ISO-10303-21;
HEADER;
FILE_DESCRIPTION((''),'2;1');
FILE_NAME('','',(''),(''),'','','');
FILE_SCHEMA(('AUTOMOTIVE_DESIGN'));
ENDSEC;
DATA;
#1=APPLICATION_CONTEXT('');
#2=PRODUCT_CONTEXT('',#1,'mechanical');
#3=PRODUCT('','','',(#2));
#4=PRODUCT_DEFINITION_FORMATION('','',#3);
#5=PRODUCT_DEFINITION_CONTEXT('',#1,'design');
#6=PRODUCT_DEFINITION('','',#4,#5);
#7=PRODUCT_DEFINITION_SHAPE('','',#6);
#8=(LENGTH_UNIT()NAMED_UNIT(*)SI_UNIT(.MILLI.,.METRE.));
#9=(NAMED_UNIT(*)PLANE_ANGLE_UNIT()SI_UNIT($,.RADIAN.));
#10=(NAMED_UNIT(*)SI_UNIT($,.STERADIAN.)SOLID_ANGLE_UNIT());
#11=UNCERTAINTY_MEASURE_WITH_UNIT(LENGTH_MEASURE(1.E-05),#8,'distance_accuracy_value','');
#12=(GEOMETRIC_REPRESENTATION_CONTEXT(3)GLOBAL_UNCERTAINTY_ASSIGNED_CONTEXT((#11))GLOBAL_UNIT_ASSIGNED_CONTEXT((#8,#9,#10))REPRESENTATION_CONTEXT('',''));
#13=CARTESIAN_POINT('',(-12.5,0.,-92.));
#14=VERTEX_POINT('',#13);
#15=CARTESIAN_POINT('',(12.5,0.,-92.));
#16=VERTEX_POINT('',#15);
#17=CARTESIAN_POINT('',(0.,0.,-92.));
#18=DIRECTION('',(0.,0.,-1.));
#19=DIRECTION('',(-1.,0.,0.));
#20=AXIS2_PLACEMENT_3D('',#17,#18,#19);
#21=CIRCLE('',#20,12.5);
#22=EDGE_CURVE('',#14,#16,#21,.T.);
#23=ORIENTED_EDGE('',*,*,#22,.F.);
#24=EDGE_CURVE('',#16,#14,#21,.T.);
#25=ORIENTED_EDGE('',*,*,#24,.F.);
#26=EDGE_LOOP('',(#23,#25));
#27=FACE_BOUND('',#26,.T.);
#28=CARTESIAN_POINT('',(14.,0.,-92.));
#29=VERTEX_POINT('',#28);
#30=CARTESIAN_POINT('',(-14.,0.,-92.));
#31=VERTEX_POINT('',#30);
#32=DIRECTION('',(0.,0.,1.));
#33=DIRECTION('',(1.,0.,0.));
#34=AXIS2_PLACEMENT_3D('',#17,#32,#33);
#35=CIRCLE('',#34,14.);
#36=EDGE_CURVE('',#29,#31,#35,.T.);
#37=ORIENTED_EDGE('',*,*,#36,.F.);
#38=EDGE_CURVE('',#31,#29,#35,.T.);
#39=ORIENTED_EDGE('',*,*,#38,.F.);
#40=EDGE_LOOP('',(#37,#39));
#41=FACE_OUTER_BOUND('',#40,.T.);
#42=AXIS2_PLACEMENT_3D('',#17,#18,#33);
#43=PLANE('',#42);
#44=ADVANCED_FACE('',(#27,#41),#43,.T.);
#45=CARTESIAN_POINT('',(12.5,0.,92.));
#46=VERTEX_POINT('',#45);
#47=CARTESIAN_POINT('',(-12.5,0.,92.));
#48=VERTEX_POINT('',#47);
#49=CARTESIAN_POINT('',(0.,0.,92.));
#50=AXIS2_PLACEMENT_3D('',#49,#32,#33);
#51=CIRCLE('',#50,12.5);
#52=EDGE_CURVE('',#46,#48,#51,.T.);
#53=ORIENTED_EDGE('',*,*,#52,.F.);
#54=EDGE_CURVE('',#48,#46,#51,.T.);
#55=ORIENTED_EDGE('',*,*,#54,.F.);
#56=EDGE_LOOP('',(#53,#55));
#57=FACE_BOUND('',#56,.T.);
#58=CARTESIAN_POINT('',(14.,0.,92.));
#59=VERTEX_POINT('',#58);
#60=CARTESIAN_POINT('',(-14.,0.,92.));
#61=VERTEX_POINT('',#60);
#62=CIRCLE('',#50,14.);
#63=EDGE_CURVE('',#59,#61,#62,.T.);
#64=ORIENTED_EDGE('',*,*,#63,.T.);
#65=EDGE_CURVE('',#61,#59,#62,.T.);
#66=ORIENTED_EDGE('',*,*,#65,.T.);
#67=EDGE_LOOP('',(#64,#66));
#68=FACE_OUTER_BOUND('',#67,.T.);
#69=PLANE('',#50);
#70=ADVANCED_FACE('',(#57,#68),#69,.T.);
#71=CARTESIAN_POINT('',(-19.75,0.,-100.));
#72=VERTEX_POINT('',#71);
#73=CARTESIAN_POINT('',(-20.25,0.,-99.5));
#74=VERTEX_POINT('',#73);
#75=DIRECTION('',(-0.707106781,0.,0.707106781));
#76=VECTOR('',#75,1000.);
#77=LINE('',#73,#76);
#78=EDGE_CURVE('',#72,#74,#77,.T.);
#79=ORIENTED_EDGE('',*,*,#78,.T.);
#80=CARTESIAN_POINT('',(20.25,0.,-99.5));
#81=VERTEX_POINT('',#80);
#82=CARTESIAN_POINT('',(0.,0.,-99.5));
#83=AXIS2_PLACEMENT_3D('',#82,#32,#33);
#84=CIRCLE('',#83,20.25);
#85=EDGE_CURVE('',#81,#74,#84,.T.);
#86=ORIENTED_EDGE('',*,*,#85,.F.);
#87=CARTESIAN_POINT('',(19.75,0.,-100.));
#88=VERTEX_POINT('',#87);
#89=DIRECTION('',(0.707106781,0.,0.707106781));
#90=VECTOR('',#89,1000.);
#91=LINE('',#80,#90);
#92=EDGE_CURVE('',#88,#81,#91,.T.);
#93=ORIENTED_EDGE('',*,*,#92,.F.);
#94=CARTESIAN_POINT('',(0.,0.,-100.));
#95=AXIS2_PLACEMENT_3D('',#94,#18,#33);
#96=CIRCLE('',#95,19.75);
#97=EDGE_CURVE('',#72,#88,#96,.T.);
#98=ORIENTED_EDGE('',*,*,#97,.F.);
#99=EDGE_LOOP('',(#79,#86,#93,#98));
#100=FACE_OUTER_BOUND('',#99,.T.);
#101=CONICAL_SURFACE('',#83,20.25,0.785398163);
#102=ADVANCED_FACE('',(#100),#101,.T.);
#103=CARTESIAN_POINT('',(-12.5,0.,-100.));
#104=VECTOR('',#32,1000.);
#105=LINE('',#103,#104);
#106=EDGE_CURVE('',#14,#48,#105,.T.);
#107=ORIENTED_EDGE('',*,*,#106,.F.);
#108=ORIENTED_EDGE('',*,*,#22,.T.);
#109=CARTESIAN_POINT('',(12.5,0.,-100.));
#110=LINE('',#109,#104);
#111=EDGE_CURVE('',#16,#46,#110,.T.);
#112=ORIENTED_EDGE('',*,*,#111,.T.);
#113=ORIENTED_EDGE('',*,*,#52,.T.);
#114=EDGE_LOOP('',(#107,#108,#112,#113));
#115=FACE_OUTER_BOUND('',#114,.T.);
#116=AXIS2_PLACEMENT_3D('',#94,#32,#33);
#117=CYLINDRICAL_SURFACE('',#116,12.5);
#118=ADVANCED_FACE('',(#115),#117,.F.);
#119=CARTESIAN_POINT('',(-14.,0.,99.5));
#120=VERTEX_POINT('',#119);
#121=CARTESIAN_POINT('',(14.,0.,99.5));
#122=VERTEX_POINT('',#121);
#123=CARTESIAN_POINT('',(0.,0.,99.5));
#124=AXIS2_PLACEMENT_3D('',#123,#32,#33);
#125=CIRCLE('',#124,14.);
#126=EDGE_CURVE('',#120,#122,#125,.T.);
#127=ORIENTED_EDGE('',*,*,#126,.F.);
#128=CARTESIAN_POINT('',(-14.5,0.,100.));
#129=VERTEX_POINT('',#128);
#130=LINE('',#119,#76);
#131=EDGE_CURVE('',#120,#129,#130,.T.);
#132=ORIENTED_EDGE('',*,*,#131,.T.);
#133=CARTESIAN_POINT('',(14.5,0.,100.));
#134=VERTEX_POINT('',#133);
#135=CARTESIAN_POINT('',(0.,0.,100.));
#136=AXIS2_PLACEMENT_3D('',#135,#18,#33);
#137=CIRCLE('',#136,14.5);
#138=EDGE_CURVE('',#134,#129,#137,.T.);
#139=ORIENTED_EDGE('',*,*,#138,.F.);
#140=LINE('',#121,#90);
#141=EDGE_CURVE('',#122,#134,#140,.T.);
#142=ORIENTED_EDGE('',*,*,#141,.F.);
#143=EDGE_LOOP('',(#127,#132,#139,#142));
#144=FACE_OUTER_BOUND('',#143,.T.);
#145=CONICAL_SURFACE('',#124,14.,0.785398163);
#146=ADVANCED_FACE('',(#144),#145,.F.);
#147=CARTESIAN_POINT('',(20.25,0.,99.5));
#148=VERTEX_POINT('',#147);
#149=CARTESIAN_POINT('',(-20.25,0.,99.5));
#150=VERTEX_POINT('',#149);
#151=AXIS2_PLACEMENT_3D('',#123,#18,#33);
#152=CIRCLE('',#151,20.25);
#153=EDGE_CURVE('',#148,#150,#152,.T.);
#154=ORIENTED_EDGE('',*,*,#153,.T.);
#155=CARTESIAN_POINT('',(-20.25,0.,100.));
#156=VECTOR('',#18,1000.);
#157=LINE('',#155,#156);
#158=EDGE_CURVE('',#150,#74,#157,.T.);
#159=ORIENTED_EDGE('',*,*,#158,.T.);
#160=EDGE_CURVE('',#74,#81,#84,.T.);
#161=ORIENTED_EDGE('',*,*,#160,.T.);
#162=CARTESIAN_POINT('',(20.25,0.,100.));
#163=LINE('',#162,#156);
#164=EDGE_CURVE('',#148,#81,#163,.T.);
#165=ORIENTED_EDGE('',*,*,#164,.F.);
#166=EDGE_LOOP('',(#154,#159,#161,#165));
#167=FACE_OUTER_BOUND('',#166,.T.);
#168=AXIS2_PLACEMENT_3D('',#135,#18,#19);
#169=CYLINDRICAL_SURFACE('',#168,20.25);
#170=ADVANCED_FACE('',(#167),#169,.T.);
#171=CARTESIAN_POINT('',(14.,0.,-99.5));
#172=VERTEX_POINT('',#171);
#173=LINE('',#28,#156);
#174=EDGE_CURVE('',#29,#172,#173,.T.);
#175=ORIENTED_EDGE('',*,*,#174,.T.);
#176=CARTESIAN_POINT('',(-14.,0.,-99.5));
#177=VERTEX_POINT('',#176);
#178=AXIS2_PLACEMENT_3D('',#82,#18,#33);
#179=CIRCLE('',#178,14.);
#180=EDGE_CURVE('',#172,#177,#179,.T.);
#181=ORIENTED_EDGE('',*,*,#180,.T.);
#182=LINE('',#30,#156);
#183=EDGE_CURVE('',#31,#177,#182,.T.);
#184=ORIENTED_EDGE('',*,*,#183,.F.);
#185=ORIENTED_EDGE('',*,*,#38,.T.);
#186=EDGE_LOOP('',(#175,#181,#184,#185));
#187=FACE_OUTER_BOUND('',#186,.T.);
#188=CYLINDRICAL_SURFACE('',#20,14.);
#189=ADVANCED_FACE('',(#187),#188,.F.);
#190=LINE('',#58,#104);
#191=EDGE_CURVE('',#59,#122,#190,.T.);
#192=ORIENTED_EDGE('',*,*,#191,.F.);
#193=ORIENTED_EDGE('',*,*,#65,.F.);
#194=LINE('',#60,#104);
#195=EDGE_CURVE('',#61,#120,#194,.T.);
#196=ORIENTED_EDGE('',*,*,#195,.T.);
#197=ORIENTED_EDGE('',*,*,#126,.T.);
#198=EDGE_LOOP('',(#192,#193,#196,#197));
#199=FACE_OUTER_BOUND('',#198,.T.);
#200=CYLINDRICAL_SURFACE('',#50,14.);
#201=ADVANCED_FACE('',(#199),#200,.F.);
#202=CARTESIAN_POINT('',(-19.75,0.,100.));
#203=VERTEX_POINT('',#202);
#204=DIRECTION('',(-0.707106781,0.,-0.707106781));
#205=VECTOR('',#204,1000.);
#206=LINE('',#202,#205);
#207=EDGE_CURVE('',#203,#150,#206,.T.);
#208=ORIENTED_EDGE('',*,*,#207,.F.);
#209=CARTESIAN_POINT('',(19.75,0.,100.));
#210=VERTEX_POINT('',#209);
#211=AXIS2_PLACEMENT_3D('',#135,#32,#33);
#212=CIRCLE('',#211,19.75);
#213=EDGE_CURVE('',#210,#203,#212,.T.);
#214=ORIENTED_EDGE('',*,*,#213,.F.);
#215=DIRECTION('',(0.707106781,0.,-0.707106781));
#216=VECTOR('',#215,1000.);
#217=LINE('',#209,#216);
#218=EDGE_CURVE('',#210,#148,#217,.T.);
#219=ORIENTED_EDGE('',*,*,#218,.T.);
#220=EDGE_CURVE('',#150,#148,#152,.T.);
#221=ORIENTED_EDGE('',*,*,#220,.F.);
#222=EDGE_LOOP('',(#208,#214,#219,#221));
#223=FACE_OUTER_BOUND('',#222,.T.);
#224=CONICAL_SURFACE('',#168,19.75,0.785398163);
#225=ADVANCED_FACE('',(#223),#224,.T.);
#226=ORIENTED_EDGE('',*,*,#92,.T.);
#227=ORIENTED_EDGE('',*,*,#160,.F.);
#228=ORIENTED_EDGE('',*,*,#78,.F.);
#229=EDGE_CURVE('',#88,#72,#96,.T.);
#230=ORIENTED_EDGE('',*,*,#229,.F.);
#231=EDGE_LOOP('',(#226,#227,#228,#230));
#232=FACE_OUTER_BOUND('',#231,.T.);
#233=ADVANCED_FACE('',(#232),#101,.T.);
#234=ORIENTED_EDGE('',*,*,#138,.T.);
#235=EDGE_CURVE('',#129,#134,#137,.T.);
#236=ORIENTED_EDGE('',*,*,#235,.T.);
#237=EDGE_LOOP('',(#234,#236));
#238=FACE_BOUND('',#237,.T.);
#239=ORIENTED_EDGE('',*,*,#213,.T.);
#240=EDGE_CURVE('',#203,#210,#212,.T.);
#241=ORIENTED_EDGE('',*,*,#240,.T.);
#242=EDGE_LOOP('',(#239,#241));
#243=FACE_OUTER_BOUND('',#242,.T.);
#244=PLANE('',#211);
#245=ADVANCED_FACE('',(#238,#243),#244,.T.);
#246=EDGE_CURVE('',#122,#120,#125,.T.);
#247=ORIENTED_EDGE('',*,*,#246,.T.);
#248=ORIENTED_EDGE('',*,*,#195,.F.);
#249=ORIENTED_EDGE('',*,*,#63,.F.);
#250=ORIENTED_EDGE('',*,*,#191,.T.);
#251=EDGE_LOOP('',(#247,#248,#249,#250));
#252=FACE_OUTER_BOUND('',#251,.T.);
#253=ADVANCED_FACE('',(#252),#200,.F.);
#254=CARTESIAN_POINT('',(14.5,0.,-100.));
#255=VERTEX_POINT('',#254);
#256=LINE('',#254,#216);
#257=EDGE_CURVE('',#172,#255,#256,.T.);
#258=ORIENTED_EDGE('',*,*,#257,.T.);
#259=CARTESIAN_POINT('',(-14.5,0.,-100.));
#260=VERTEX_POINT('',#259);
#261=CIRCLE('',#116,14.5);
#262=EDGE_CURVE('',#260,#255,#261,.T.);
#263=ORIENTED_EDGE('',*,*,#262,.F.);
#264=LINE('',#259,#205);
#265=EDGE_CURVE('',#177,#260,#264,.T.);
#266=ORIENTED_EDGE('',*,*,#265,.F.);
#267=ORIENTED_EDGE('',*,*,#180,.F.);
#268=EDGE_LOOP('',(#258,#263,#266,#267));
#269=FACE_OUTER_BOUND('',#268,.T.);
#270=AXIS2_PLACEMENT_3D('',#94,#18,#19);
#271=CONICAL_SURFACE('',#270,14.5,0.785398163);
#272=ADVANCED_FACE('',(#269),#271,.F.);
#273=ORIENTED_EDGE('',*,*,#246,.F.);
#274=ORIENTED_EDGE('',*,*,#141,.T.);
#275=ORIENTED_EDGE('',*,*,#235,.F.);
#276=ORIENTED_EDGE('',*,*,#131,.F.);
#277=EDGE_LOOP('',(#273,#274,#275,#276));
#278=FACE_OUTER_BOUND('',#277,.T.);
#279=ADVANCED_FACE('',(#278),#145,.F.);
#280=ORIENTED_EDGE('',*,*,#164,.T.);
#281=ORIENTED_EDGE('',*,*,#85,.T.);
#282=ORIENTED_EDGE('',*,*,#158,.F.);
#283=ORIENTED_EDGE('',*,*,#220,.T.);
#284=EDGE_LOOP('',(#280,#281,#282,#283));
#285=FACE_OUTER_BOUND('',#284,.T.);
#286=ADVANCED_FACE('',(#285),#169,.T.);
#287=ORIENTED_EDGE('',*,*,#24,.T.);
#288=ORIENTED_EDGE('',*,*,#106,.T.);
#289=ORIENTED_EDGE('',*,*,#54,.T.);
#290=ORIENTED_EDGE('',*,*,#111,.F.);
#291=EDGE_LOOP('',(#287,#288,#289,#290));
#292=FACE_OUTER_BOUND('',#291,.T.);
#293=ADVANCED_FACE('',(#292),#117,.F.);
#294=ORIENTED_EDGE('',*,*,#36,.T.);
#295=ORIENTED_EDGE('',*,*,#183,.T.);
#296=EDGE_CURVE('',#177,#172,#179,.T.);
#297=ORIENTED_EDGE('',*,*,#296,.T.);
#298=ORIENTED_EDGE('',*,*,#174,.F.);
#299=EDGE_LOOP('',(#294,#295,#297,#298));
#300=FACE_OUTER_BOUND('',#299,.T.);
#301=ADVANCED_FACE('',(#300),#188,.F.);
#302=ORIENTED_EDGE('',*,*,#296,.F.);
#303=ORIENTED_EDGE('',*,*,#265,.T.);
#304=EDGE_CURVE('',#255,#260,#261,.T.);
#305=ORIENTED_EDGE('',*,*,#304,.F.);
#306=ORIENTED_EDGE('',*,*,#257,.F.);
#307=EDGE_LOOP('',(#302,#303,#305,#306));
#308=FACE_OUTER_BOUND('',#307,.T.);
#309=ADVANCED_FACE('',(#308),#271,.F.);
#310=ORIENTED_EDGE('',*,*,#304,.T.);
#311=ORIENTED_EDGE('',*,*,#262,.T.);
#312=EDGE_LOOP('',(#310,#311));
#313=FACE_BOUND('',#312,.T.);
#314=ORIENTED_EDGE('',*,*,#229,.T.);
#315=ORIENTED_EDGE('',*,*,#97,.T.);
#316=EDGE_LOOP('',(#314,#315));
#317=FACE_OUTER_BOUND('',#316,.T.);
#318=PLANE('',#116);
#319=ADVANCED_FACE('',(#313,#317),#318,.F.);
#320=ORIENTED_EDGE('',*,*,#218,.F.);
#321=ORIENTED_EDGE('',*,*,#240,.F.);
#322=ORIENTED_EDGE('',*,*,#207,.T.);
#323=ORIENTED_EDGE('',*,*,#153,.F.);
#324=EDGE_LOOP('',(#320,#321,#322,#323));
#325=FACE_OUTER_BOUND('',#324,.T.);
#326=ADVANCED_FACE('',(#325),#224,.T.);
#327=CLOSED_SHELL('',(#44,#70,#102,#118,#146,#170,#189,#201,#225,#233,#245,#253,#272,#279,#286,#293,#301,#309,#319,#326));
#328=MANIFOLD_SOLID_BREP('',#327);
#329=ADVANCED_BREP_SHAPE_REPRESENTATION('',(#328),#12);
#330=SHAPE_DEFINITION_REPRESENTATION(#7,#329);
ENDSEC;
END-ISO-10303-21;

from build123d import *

# Parameters (mm, degrees)
SKETCH_1_R          = 20.25
EXTRUDE_1_DEPTH     = 100
SKETCH_2_R          = 14
CUT_EXTRUDE_1_DEPTH = 8
SKETCH_3_R          = 12.5
CUT_EXTRUDE_2_DEPTH = 195.12399388
CHAMFER_1_SIZE      = 0.5


with BuildPart() as part:
    # 草图1 → 凸台-拉伸1 (new, symmetric)
    with BuildSketch(Plane.XY):
        Circle(SKETCH_1_R)
    extrude(amount=EXTRUDE_1_DEPTH, both=True)

    # 草图2 → 切除-拉伸1 (cut)
    with BuildSketch(Plane.XY.offset(100)):
        Circle(SKETCH_2_R)
    cut_extrude_1 = extrude(amount=-CUT_EXTRUDE_1_DEPTH, mode=Mode.SUBTRACT)

    # 镜向1: 切除-拉伸1 across plane
    add(cut_extrude_1.mirror(Plane.XY), mode=Mode.SUBTRACT)

    # 草图3 → 切除-拉伸2 (cut, through all)
    with BuildSketch(Plane.XY.offset(92)):
        Circle(SKETCH_3_R)
    extrude(amount=-CUT_EXTRUDE_2_DEPTH, mode=Mode.SUBTRACT)

    # 倒角1
    chamfer_1_edges = [part.edges().sort_by_distance(p)[0] for p in [
        (-14, 0, -100),
        (-20.25, 0, -100),
        (-20.25, 0, 100),
        (-14, 0, 100),
    ]]
    chamfer(chamfer_1_edges, length=CHAMFER_1_SIZE)


solid = part.part
